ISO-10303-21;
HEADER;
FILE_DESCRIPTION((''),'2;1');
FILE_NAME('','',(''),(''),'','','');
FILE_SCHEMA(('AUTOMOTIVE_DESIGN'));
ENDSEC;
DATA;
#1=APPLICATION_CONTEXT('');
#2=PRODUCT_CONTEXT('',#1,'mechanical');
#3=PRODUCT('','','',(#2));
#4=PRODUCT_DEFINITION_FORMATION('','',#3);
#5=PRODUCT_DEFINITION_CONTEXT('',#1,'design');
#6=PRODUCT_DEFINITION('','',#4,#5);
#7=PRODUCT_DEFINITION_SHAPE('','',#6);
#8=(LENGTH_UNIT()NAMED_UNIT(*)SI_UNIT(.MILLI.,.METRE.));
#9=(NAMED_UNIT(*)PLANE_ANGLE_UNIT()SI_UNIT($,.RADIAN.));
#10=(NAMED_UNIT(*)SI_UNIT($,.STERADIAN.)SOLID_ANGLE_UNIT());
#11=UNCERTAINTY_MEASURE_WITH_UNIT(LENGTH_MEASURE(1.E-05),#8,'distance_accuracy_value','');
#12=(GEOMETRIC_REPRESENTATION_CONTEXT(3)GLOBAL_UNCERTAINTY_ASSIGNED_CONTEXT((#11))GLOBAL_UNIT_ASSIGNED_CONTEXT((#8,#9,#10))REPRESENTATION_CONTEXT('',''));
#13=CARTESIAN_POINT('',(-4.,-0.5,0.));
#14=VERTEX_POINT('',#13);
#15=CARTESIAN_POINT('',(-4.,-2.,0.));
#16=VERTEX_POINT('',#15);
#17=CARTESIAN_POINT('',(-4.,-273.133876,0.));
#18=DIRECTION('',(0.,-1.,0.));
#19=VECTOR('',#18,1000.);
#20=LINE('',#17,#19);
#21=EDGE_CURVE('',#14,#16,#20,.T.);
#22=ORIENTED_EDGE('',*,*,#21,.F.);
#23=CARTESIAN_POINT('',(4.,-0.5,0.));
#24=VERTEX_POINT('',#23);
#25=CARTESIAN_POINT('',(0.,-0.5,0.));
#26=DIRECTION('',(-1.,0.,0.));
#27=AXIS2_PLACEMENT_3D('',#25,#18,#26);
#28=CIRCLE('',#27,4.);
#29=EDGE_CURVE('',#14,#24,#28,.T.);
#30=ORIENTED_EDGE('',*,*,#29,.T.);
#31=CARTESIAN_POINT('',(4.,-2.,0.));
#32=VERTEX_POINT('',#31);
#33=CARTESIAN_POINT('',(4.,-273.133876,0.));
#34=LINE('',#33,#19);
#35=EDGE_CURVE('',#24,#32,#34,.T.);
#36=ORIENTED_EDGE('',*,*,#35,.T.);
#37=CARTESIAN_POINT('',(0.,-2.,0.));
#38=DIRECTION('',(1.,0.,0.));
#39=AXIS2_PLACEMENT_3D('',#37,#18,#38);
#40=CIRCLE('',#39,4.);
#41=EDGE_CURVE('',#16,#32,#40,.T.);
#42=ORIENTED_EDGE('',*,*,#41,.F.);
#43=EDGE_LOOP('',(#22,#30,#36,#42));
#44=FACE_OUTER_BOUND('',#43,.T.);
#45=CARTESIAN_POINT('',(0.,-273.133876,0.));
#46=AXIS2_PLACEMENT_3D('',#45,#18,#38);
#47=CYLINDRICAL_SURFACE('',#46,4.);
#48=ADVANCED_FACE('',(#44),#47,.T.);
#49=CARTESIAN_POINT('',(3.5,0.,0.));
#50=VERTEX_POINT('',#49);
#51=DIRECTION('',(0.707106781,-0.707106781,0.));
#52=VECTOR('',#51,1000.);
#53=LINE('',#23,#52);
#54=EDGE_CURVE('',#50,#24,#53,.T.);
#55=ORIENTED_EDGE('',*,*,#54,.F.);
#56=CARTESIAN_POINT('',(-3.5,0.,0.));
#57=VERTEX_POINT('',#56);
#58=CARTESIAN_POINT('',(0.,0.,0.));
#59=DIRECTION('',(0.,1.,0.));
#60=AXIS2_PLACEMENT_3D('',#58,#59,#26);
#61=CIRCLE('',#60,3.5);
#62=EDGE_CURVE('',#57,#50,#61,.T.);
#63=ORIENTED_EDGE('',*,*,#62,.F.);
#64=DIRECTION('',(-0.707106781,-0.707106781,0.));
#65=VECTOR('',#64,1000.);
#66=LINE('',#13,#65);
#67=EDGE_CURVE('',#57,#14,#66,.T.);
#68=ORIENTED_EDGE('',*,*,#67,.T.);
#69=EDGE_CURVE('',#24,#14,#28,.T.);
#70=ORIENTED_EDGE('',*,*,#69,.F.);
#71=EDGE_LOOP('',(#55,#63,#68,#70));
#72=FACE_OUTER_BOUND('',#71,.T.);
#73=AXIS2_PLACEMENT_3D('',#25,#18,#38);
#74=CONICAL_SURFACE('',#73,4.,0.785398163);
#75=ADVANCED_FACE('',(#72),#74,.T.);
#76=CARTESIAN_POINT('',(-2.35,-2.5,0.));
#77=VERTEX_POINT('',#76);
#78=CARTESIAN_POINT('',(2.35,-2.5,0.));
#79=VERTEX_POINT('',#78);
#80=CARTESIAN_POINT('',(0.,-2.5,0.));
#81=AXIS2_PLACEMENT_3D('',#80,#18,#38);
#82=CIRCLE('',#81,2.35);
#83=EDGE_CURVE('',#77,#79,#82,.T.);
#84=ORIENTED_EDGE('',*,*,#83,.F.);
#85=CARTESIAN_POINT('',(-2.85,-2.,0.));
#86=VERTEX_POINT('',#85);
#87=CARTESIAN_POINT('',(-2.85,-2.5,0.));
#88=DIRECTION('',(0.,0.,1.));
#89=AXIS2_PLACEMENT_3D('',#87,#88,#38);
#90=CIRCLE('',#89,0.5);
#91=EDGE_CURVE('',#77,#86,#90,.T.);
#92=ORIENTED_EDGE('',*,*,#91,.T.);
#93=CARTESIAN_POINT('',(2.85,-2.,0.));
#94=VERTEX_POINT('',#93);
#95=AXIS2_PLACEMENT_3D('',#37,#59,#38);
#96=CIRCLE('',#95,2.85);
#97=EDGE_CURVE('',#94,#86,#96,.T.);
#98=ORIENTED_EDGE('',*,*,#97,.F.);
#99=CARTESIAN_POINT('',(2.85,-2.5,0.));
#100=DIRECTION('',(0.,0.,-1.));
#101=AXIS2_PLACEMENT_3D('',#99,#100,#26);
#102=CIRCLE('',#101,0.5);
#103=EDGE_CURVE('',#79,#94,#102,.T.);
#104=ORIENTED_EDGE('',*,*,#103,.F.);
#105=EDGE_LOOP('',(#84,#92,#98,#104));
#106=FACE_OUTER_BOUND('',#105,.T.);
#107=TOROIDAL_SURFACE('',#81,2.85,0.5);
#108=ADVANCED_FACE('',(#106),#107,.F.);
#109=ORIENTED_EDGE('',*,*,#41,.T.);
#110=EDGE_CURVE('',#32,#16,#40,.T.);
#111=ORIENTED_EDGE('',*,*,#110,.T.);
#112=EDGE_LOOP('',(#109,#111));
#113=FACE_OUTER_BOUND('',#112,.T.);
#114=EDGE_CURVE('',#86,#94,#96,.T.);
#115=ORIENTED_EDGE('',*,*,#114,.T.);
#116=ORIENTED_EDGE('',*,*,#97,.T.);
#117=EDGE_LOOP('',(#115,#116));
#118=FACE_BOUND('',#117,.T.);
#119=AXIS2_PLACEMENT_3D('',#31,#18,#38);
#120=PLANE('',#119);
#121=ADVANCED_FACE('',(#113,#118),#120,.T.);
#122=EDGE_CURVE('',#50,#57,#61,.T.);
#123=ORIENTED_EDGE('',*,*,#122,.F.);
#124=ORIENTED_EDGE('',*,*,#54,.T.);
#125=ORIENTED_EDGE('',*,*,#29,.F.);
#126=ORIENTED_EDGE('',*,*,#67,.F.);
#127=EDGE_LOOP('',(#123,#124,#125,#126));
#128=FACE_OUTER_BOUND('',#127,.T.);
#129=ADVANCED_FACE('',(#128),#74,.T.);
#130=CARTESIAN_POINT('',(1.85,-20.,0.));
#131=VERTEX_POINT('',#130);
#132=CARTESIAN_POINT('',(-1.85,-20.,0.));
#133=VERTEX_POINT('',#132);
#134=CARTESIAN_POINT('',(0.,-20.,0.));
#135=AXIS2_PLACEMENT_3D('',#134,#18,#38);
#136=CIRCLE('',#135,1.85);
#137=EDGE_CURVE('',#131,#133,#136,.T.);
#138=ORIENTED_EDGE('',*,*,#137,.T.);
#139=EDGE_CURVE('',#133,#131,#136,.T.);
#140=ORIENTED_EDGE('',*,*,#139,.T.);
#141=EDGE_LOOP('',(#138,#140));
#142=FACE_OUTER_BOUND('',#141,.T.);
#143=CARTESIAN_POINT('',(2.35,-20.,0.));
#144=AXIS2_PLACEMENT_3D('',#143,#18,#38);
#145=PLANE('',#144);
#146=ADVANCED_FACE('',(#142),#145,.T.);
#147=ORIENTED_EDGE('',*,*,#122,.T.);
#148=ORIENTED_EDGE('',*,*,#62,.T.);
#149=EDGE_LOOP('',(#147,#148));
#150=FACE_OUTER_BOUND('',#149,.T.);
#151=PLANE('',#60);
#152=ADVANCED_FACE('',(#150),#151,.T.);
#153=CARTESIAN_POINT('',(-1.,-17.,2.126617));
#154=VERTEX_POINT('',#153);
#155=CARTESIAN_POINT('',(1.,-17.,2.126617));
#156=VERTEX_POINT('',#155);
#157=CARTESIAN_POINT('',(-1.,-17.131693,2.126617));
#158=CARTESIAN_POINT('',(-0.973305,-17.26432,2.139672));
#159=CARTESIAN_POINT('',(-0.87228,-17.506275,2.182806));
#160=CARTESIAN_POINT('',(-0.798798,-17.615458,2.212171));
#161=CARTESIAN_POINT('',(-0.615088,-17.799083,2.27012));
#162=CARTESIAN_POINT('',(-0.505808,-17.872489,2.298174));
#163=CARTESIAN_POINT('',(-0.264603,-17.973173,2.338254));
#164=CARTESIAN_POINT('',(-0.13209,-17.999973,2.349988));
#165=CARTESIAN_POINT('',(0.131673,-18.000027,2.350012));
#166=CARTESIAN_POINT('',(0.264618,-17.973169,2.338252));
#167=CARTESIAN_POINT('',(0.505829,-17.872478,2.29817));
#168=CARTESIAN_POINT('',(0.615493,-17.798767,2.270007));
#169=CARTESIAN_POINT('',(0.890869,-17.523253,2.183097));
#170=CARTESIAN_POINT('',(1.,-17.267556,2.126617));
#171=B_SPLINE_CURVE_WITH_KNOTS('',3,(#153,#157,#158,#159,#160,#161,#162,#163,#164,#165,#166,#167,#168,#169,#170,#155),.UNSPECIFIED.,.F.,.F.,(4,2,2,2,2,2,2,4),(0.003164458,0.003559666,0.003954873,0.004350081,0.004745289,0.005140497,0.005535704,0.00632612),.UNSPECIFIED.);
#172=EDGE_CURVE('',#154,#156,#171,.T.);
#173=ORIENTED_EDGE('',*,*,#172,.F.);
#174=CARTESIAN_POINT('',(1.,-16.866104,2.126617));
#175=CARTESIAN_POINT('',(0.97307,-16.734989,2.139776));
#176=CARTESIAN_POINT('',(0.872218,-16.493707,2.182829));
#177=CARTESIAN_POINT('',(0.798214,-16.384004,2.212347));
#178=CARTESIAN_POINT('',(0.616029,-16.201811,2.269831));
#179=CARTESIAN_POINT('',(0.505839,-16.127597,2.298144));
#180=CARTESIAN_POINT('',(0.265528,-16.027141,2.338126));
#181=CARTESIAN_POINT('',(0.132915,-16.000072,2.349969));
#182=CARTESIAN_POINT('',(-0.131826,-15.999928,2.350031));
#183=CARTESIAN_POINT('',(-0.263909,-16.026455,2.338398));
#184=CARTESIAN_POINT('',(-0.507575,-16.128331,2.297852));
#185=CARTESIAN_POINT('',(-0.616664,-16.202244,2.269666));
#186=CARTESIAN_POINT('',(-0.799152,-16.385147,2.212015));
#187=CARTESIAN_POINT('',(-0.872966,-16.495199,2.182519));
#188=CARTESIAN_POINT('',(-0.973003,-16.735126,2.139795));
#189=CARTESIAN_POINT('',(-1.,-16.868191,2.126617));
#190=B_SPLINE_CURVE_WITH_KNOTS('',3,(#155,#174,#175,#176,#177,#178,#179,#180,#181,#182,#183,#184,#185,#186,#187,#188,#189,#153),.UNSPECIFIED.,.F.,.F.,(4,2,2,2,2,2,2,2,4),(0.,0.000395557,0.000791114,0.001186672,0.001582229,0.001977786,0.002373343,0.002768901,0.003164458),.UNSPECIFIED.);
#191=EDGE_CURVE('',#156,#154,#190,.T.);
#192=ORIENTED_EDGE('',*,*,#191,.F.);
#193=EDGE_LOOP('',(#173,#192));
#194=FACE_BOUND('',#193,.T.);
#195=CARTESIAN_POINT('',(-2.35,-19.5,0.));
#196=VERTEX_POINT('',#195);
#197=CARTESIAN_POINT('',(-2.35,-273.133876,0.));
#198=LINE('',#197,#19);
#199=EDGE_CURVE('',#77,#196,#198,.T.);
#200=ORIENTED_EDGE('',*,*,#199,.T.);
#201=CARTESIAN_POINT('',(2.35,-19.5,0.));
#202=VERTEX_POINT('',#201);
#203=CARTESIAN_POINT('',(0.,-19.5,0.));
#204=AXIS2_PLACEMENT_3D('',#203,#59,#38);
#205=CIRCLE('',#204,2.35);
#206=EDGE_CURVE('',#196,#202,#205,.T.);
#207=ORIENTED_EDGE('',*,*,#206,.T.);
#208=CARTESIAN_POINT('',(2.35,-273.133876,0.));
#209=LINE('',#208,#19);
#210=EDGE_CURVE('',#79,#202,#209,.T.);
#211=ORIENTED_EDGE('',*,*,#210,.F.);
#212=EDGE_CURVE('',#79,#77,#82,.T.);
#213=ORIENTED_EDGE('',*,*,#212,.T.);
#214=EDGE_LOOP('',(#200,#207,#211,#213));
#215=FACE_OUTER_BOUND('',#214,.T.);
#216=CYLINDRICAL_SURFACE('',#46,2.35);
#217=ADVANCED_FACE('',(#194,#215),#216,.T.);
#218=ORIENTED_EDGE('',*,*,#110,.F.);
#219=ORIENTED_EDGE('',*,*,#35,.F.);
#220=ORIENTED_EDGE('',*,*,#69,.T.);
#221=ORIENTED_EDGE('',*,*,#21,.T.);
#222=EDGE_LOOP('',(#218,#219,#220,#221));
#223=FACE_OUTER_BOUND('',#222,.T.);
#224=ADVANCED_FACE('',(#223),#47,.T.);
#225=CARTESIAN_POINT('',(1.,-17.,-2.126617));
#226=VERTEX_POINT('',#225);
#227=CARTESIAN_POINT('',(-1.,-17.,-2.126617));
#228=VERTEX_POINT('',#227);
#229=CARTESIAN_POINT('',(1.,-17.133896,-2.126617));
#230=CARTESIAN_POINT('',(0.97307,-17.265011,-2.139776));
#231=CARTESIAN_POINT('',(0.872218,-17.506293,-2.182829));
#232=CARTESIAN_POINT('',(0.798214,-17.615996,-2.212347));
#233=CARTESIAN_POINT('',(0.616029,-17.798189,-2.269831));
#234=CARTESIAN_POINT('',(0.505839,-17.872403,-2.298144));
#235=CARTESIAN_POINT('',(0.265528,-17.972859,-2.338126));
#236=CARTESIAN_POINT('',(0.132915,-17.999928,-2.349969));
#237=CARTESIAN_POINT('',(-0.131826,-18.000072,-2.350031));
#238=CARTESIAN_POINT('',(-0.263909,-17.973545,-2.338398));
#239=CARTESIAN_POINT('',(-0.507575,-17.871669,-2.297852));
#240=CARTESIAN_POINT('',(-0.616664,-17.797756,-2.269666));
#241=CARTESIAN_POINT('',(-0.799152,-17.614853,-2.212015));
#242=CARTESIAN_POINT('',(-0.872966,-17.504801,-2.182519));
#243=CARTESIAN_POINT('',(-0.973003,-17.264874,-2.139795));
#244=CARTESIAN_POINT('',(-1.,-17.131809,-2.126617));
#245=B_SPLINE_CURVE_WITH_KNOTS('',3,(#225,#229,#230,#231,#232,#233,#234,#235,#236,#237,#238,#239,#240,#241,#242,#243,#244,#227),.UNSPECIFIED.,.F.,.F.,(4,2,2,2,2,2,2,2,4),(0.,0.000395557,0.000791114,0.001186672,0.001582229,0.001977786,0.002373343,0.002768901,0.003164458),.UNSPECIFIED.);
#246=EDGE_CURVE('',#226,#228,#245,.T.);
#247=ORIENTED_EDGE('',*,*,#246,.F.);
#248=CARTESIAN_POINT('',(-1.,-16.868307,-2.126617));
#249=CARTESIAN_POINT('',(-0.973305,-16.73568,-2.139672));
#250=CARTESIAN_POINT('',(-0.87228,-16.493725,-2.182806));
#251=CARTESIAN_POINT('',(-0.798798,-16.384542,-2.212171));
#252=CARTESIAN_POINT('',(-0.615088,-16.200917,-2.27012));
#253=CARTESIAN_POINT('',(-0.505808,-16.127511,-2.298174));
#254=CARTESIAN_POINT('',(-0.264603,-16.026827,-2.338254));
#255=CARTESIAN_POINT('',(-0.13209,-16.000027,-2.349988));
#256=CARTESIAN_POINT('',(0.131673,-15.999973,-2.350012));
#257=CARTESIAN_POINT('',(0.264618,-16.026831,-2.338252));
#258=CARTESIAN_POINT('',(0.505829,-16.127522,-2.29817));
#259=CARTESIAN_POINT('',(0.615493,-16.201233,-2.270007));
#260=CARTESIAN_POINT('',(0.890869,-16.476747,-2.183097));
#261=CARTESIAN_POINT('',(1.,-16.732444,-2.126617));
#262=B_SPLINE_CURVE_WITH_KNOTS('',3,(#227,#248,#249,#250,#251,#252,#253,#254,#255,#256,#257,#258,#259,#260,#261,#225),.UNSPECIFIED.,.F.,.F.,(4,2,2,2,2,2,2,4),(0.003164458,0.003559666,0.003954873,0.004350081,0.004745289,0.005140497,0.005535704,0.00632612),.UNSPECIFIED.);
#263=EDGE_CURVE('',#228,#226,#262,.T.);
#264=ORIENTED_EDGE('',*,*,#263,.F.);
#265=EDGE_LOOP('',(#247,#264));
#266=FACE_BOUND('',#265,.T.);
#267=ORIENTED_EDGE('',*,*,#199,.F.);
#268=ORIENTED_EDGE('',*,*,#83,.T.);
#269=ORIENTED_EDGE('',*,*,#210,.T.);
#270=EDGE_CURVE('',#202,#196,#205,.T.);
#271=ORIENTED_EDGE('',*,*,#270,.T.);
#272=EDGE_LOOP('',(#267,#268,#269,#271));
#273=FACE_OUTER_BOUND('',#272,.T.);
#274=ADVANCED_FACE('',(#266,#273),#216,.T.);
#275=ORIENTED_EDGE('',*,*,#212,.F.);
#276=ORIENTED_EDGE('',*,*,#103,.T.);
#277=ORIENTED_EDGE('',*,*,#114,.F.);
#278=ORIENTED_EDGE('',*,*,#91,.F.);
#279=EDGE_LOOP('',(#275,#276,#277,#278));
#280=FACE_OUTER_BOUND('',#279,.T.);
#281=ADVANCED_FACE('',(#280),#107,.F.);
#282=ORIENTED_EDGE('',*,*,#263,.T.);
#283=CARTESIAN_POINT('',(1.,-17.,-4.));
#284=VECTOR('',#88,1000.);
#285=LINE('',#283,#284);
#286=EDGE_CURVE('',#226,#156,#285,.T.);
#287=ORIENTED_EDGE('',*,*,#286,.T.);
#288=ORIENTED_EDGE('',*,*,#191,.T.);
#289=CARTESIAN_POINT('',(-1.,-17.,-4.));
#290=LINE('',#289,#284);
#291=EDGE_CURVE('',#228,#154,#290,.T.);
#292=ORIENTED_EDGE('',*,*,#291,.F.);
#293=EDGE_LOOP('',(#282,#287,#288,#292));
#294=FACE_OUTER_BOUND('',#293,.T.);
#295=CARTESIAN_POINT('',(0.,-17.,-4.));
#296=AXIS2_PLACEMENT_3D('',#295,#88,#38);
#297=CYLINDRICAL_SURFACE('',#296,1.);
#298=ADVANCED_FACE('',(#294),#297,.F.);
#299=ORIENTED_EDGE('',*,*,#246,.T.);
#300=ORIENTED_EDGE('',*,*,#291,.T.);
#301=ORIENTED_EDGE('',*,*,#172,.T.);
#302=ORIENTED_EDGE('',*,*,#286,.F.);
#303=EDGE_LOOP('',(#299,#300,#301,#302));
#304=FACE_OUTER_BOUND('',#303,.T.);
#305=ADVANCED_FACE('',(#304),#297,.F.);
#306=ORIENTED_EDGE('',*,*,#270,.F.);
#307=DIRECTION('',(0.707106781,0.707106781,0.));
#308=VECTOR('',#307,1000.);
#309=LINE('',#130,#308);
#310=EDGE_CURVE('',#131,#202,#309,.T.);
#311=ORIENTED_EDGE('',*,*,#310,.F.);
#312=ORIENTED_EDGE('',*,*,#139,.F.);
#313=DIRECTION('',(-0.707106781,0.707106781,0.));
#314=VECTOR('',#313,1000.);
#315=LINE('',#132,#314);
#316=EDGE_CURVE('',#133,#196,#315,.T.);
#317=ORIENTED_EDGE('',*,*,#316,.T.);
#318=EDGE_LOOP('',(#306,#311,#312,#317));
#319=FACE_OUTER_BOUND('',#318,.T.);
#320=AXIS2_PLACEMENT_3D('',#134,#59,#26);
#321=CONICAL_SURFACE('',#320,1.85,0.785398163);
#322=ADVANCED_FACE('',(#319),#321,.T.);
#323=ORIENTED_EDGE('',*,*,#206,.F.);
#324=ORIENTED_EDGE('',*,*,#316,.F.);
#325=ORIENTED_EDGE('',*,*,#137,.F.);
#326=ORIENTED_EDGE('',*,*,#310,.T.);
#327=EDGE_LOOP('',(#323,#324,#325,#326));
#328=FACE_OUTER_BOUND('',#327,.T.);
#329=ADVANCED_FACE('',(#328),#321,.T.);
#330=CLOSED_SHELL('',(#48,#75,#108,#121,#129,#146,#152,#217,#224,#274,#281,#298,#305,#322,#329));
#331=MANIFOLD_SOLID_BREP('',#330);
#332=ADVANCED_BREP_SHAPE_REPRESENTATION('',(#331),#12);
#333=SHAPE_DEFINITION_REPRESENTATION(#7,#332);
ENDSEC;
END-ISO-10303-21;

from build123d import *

# Parameters (mm, degrees)
FILLET1_R               = 0.5
CHAMFER1_SIZE           = 0.5
CUT_EXTRUDE1_DEPTH      = 21.784609691
CUT_EXTRUDE1_DEPTH_BACK = 21.784609691
SKETCH2_R               = 1


with BuildPart() as part:
    # Sketch1 → Revolve1 (revolve)
    with BuildSketch(Plane.XY):
        Polygon((0, 0), (4, 0), (4, -2), (2.35, -2), (2.35, -20), (0, -20), align=None)
    revolve(axis=Axis((0, -273.133875929, 0), (0, 1, 0)))

    # Fillet1
    fillet1_edges = [part.edges().sort_by_distance(p)[0] for p in [
        (-2.35, -2, 0),
    ]]
    fillet(fillet1_edges, radius=FILLET1_R)

    # Chamfer1
    chamfer1_edges = [part.edges().sort_by_distance(p)[0] for p in [
        (-2.35, -20, 0),
        (-4, 0, 0),
    ]]
    chamfer(chamfer1_edges, length=CHAMFER1_SIZE)

    # Sketch2 → Cut-Extrude1 (cut, two sides: drawn at the far end of the back side and taken through both)
    with BuildSketch(Plane.XY.offset(-CUT_EXTRUDE1_DEPTH_BACK)):
        with Locations((0, -17)):
            Circle(SKETCH2_R)
    extrude(amount=CUT_EXTRUDE1_DEPTH + CUT_EXTRUDE1_DEPTH_BACK, mode=Mode.SUBTRACT)


solid = part.part
